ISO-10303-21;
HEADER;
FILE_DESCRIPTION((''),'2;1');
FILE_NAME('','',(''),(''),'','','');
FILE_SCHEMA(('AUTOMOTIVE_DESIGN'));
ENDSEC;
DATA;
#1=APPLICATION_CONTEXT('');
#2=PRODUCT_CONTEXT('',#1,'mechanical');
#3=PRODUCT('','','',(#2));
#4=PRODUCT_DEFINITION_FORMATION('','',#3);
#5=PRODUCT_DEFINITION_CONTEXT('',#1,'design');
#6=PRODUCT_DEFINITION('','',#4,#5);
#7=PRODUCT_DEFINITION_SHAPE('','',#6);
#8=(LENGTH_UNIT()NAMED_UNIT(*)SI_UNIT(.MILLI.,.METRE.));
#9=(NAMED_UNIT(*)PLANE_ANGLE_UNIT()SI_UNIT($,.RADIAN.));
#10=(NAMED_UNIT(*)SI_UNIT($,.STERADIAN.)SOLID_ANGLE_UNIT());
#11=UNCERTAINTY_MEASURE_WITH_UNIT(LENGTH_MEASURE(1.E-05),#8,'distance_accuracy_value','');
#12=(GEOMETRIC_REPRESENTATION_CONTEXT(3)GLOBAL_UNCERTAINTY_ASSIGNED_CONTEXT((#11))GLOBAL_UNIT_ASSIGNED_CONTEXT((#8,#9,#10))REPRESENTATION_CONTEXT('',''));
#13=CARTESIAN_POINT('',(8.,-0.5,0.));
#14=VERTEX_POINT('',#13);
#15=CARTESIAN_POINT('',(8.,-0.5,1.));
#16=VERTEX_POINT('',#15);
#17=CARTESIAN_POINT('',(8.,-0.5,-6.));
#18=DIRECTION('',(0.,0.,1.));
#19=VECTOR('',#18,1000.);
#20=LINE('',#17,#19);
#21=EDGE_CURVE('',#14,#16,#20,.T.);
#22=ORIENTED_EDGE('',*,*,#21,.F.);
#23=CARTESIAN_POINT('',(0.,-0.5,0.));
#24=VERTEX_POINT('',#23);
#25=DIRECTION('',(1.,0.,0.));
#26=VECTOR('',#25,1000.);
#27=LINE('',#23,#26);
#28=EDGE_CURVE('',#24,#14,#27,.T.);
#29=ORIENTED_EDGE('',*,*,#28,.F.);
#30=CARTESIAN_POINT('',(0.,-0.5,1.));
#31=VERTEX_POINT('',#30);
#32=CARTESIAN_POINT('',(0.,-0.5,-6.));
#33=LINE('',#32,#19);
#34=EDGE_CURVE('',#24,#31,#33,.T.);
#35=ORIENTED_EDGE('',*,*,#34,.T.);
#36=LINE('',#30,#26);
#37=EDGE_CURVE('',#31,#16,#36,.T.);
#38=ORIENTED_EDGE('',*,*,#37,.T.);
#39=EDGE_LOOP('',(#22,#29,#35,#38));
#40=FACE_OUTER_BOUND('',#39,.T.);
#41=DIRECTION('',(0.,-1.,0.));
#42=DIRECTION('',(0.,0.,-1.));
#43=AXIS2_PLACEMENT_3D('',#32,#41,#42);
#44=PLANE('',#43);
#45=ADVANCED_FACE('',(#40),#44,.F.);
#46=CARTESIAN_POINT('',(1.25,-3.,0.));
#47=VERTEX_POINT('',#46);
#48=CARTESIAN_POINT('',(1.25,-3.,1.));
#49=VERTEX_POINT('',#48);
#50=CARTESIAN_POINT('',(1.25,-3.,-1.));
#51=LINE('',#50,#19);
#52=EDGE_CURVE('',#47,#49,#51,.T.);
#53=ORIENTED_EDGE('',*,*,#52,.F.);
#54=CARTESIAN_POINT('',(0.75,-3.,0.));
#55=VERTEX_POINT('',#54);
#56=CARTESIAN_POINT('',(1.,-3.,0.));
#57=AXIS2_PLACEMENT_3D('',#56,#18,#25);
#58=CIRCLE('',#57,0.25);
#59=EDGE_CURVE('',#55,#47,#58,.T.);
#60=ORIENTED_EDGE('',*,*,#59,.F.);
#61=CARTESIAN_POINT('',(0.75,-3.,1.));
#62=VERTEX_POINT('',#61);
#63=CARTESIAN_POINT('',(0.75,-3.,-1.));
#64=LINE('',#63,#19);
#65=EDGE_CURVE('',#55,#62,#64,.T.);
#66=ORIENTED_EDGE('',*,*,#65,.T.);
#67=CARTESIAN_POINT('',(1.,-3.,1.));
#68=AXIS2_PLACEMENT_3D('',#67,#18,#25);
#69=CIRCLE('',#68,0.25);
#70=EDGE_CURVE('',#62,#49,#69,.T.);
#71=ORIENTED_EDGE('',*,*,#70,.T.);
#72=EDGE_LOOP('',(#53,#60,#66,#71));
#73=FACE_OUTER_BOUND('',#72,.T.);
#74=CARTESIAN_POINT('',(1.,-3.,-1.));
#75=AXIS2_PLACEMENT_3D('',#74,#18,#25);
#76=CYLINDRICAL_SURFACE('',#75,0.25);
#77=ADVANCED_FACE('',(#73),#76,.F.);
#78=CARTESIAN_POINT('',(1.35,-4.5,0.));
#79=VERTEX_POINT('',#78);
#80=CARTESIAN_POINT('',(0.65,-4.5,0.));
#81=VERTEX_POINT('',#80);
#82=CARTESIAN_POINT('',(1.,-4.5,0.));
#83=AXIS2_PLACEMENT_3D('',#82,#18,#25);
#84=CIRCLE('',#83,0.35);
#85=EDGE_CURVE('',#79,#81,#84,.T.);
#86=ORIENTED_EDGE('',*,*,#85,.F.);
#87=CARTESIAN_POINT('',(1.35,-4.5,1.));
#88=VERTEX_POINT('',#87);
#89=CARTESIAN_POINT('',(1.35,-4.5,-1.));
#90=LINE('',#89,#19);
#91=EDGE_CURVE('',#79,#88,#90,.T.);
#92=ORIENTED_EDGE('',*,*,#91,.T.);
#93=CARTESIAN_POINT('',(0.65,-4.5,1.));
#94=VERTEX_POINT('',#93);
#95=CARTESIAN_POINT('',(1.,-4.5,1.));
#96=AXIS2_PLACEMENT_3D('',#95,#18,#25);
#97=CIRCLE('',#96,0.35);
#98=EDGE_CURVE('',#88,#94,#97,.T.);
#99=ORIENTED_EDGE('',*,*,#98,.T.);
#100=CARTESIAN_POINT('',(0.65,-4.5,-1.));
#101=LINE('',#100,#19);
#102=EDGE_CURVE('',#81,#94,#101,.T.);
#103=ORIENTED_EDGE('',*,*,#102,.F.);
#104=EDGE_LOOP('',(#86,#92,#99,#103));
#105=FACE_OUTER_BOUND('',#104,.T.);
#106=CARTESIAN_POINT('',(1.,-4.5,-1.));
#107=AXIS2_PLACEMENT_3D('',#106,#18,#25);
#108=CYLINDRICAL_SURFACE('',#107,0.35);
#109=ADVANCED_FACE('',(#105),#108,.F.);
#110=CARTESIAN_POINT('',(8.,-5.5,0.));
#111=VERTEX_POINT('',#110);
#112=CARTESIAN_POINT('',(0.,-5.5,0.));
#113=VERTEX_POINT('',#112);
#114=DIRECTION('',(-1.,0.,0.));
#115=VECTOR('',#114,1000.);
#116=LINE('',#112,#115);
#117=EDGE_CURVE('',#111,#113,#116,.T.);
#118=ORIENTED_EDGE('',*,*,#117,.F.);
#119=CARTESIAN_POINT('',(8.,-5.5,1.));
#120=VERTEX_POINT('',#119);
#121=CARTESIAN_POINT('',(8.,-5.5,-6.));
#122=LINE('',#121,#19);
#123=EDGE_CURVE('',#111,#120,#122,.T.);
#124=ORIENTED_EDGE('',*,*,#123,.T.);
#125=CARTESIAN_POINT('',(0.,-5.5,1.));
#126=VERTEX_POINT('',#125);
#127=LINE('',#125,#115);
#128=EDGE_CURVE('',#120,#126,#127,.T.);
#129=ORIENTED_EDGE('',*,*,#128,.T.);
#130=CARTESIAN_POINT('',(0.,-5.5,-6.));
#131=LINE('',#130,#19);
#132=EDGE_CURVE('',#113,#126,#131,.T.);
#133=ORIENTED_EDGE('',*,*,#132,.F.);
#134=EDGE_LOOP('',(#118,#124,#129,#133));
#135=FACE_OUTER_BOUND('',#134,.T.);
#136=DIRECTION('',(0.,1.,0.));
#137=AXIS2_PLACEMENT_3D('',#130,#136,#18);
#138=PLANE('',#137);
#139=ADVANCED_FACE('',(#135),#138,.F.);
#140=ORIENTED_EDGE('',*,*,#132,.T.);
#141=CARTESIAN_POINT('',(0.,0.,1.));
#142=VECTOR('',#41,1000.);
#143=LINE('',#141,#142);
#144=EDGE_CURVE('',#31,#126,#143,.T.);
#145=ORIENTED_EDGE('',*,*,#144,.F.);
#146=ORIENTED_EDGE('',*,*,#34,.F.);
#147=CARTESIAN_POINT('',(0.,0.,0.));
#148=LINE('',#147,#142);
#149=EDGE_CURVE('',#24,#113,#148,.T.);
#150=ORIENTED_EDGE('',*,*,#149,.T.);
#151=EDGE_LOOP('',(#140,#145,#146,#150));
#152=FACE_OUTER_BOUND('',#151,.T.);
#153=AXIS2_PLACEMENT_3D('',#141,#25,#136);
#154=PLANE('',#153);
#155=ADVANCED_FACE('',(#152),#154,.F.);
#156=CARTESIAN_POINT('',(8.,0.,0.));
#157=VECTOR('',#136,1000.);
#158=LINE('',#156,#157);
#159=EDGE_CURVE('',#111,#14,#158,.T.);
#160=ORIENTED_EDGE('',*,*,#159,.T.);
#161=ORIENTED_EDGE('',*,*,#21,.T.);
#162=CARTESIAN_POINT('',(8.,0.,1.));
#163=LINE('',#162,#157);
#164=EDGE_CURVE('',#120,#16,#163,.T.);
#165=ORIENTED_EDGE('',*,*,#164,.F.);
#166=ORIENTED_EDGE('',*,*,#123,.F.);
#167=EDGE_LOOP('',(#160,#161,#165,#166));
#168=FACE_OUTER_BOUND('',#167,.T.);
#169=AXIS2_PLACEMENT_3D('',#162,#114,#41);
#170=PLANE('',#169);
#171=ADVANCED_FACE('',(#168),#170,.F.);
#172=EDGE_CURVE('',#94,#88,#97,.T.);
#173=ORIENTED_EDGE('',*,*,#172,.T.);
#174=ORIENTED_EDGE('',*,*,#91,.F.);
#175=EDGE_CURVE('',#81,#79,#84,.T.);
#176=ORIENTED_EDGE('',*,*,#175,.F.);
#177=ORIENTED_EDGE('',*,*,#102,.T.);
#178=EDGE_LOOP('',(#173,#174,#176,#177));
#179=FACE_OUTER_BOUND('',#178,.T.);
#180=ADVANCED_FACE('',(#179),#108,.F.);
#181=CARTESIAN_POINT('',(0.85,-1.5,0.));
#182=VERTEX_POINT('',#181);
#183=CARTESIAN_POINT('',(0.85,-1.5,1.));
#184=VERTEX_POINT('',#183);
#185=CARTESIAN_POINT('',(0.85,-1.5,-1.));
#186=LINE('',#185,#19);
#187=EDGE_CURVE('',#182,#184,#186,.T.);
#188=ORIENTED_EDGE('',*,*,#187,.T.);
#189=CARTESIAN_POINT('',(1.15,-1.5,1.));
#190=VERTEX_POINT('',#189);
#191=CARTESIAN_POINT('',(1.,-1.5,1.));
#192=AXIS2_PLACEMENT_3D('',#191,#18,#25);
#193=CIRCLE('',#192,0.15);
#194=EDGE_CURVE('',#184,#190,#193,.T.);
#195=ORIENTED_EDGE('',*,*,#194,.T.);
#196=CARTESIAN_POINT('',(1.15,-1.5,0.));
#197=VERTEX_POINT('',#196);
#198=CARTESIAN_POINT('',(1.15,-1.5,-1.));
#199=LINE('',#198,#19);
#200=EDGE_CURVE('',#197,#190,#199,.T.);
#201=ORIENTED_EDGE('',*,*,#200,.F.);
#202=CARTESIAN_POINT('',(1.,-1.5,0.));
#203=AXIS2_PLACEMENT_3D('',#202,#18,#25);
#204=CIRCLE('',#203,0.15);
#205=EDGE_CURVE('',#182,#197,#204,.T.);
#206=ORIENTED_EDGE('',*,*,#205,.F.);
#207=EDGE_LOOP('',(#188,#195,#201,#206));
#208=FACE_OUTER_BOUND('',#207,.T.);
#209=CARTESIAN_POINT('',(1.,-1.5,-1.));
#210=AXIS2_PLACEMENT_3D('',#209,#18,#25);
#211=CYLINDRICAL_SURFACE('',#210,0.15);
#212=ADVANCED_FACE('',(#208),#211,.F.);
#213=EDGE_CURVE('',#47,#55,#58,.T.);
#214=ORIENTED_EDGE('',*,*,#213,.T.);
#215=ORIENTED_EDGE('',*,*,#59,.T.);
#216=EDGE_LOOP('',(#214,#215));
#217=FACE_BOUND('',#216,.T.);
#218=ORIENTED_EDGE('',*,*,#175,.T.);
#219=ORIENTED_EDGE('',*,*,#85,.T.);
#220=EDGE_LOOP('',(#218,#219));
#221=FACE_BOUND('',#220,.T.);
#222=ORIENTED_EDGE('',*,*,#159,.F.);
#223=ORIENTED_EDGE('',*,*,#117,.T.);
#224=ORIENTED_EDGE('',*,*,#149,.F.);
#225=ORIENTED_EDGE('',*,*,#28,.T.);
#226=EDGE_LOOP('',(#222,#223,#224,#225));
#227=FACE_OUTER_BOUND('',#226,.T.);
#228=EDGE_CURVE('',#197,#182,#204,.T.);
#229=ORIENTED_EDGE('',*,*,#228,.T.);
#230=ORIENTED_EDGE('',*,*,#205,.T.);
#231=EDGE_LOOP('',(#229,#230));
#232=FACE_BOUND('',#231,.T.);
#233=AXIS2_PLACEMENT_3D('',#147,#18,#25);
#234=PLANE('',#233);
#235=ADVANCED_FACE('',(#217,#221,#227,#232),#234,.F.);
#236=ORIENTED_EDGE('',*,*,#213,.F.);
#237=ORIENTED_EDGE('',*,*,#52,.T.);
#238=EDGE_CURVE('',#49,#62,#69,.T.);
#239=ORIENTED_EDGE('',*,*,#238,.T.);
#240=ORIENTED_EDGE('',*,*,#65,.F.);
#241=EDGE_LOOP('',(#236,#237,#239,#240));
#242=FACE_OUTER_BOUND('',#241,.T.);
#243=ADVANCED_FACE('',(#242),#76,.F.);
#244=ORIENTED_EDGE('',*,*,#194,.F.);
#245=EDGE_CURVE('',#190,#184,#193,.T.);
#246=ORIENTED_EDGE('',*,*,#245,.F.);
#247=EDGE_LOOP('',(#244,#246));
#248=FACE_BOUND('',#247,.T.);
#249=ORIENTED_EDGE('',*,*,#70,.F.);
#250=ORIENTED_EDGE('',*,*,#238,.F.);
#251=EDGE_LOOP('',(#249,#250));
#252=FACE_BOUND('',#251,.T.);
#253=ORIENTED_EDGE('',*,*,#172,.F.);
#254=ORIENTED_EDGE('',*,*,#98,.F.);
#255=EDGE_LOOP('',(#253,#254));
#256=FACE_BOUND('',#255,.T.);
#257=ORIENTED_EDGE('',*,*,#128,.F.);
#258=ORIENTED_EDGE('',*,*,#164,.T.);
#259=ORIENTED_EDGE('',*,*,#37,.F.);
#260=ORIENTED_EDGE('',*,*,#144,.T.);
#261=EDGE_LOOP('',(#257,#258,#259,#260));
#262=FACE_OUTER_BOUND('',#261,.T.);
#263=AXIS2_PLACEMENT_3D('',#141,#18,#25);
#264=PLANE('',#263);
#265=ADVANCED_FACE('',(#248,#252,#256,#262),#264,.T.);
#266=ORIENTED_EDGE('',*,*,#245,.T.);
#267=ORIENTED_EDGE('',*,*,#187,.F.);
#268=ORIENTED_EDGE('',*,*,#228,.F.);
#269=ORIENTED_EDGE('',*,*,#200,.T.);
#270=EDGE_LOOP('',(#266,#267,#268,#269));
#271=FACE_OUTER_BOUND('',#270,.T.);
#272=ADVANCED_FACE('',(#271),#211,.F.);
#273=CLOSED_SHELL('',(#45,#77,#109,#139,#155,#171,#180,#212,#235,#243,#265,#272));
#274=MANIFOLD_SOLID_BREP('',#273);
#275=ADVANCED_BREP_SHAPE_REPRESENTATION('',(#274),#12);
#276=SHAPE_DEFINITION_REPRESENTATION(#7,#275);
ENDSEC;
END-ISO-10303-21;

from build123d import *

# Parameters (mm, degrees)
SKETCH1_W           = 8
SKETCH1_H           = 6
BOSS_EXTRUDE1_DEPTH = 1
SKETCH2_R           = 0.15
SKETCH2_R_2         = 0.25
SKETCH2_R_3         = 0.35
CUT_EXTRUDE1_DEPTH  = 2
SKETCH3_W           = 8
SKETCH3_H           = 0.5
CUT_EXTRUDE2_DEPTH  = 7


with BuildPart() as part:
    # Sketch1 → Boss-Extrude1 (new body)
    with BuildSketch(Plane.XY):
        with Locations((4, -3)):
            Rectangle(SKETCH1_W, SKETCH1_H)
    extrude(amount=BOSS_EXTRUDE1_DEPTH)

    # Sketch2 → Cut-Extrude1 (cut)
    with BuildSketch(Plane.XY.offset(1)):
        with Locations((1, -1.5)):
            Circle(SKETCH2_R)
        with Locations((1, -3)):
            Circle(SKETCH2_R_2)
        with Locations((1, -4.5)):
            Circle(SKETCH2_R_3)
    extrude(amount=-CUT_EXTRUDE1_DEPTH, mode=Mode.SUBTRACT)

    # Sketch3 → Cut-Extrude2 (cut)
    with BuildSketch(Plane.XY.offset(1)):
        with Locations((4, -0.25)):
            Rectangle(SKETCH3_W, SKETCH3_H)
        with Locations((4, -5.75)):
            Rectangle(SKETCH3_W, SKETCH3_H)
    extrude(amount=-CUT_EXTRUDE2_DEPTH, mode=Mode.SUBTRACT)


solid = part.part
